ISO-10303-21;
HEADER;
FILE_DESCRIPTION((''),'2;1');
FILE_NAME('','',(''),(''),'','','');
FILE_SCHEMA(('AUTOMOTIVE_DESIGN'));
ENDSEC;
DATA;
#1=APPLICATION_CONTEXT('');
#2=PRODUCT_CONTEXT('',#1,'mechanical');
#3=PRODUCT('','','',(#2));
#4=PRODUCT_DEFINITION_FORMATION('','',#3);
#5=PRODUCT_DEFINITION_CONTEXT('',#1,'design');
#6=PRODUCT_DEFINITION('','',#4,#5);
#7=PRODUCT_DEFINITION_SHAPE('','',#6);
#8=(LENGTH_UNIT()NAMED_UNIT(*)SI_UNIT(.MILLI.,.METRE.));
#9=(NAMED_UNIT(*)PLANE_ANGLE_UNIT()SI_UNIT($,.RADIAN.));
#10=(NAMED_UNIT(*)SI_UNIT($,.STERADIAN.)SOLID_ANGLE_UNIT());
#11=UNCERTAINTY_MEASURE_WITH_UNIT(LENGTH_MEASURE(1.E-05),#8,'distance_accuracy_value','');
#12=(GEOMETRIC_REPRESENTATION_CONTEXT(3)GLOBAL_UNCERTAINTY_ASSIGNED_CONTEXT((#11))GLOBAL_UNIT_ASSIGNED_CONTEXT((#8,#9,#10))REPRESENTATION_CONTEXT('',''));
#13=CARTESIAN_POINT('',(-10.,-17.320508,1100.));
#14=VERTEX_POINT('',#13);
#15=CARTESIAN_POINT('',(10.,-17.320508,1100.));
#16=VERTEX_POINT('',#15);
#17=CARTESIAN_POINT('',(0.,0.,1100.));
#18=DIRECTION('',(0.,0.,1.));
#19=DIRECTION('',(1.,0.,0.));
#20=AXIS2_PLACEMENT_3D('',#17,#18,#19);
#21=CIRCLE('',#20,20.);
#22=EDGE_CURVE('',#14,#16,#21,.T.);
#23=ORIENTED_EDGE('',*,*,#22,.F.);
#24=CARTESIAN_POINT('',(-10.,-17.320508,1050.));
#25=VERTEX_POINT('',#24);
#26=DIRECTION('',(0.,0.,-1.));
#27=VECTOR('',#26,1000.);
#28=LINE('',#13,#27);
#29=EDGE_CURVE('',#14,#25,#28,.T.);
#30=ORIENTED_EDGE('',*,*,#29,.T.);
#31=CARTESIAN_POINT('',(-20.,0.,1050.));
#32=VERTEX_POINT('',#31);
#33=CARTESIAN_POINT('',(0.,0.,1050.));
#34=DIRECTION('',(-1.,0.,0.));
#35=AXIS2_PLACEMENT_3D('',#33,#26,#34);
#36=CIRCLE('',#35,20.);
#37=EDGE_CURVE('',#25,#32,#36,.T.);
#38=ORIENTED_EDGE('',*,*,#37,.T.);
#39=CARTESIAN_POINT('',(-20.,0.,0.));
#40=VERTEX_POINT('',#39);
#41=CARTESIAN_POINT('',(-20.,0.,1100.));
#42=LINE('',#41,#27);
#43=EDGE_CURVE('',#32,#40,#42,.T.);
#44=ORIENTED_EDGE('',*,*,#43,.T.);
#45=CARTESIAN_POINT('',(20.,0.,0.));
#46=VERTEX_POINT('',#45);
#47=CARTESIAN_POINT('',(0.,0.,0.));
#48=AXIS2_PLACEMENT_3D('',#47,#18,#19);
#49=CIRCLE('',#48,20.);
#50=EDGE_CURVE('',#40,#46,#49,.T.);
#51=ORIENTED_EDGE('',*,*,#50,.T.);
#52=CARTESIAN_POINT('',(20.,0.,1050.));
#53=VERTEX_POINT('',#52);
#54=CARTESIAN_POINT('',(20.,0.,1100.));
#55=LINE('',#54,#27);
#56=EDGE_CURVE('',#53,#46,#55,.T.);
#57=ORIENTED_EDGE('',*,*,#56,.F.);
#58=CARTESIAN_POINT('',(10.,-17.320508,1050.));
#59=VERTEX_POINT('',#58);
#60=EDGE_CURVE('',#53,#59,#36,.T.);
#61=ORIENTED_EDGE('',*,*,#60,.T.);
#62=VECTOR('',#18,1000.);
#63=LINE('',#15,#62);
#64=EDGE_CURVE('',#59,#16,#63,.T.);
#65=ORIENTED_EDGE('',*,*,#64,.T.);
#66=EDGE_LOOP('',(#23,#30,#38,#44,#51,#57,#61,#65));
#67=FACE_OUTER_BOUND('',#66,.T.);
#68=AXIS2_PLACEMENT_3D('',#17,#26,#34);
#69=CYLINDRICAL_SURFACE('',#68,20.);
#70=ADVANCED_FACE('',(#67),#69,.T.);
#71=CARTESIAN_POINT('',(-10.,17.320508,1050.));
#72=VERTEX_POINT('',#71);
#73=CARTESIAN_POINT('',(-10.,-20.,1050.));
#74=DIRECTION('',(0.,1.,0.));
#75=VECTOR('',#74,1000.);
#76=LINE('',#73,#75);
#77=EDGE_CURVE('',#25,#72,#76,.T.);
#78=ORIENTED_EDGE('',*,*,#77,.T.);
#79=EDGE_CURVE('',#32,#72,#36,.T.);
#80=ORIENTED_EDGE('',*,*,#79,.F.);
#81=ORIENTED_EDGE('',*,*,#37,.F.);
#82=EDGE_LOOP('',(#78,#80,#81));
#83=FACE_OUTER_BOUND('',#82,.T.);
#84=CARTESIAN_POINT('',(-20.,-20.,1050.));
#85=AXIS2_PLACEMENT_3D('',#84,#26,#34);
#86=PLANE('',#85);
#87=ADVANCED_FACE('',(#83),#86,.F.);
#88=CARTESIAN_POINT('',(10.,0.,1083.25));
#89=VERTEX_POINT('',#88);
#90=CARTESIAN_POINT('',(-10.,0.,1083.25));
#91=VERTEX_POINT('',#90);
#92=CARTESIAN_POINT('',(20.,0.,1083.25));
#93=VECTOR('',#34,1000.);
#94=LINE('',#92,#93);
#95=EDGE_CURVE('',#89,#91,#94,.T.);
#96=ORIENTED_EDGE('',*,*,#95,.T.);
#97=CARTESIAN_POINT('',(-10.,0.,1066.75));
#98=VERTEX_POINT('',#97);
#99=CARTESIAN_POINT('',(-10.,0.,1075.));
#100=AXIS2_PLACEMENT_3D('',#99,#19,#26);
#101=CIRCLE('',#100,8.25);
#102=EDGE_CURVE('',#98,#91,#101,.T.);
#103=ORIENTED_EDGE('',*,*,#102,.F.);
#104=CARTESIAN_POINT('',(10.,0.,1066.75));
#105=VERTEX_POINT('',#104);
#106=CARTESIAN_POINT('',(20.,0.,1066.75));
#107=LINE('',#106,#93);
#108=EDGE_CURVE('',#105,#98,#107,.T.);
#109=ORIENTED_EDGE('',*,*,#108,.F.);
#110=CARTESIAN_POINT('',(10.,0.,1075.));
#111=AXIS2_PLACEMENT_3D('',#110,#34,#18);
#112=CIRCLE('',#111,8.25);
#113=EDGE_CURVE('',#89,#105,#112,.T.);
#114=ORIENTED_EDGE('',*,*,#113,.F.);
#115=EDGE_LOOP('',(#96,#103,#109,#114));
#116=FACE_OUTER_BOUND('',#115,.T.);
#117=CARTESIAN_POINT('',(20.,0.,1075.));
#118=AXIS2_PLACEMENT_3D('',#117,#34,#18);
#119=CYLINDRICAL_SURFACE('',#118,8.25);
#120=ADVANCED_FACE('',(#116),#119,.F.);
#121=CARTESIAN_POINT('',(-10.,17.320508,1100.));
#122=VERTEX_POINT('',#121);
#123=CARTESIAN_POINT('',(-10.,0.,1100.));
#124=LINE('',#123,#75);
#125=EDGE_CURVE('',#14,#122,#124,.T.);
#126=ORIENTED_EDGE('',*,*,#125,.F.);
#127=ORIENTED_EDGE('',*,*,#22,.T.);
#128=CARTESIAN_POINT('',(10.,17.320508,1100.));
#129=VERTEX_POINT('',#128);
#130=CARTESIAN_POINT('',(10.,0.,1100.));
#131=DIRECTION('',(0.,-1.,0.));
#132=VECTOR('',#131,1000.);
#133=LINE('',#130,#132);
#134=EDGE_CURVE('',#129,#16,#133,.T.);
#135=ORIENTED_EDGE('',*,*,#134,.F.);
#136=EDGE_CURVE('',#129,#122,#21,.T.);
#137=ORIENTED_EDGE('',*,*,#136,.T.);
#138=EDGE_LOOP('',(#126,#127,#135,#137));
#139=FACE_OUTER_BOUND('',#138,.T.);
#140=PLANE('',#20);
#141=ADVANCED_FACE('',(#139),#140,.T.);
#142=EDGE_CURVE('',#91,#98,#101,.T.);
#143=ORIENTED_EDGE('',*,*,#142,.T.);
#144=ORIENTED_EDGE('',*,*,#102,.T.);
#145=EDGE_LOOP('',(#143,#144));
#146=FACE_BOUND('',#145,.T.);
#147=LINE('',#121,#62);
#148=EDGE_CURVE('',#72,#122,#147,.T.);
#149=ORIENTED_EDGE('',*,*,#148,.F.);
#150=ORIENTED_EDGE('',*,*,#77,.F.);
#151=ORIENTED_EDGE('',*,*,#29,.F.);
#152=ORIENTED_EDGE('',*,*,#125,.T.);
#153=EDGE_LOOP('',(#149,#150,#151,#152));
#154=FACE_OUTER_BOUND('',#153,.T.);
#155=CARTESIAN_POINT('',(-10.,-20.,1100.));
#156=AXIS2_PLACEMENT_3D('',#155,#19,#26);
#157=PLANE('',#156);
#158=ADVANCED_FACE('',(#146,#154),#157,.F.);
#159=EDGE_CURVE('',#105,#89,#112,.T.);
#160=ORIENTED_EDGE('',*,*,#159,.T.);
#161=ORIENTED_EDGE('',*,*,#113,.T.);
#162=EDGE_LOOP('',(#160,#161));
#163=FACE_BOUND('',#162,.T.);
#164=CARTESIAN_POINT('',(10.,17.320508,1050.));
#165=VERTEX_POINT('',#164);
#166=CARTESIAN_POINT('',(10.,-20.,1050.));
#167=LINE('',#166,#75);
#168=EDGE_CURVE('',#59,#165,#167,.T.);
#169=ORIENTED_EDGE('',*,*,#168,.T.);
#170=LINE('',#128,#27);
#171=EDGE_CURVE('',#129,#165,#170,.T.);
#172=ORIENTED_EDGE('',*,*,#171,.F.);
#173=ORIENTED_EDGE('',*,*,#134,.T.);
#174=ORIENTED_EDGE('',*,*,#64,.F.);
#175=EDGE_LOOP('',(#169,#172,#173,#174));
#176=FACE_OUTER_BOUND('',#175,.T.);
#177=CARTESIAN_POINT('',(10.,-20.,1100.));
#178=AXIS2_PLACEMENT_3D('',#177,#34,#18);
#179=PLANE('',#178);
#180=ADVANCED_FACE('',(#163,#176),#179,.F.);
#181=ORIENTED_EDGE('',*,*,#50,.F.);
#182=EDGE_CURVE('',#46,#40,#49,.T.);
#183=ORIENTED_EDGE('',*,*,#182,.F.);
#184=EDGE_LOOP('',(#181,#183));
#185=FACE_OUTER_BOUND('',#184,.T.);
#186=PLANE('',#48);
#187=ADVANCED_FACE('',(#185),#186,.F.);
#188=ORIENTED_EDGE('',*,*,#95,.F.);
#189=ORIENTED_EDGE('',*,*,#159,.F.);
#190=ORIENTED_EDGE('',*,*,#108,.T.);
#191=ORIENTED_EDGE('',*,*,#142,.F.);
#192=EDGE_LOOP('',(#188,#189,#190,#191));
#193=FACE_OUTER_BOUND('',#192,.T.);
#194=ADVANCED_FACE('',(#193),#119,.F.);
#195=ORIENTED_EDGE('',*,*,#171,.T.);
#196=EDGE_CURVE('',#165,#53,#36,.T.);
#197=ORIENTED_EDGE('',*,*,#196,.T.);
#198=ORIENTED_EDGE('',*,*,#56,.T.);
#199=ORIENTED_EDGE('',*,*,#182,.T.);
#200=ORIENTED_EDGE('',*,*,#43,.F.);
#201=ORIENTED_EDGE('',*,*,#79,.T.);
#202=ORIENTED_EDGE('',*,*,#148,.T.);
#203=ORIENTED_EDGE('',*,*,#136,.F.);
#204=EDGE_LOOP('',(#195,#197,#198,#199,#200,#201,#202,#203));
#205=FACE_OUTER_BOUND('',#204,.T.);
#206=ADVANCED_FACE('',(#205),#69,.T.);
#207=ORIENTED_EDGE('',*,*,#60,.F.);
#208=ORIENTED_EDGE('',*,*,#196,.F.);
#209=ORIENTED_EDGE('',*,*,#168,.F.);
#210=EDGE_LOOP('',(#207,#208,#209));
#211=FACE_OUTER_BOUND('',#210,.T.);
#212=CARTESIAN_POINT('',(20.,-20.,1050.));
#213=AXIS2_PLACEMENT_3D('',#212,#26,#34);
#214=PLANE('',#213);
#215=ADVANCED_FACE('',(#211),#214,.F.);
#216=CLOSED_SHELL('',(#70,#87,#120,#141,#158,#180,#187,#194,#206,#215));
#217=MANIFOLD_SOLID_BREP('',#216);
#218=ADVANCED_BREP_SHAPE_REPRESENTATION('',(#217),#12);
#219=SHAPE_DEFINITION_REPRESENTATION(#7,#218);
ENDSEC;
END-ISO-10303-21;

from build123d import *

# Parameters (mm, degrees)
SKETCH1_R               = 20
BOSS_EXTRUDE1_DEPTH     = 1100
CUT_EXTRUDE1_DEPTH      = 1101.363576278
CUT_EXTRUDE1_DEPTH_BACK = 1101.363576278
SKETCH2_W               = 10
SKETCH2_H               = 50
CUT_EXTRUDE2_DEPTH      = 1101.590750461
CUT_EXTRUDE2_DEPTH_BACK = 1101.590750461
SKETCH3_R               = 8.25


with BuildPart() as part:
    # Sketch1 → Boss-Extrude1 (new body)
    with BuildSketch(Plane.XY):
        Circle(SKETCH1_R)
    extrude(amount=BOSS_EXTRUDE1_DEPTH)

    # Sketch2 → Cut-Extrude1 (cut, two sides: drawn at the far end of the back side and taken through both)
    with BuildSketch(Plane(origin=(0, 0, 0), x_dir=(1, 0, 0), z_dir=(0, 1, 0)).offset(-CUT_EXTRUDE1_DEPTH_BACK)):
        with Locations((-15, -1075)):
            Rectangle(SKETCH2_W, SKETCH2_H)
        with Locations((15, -1075)):
            Rectangle(SKETCH2_W, SKETCH2_H)
    extrude(amount=CUT_EXTRUDE1_DEPTH + CUT_EXTRUDE1_DEPTH_BACK, mode=Mode.SUBTRACT)

    # Sketch3 → Cut-Extrude2 (cut, two sides: drawn at the far end of the back side and taken through both)
    with BuildSketch(Plane.ZY.offset(10).offset(-CUT_EXTRUDE2_DEPTH_BACK)):
        with Locations((1075, 0)):
            Circle(SKETCH3_R)
    extrude(amount=CUT_EXTRUDE2_DEPTH + CUT_EXTRUDE2_DEPTH_BACK, mode=Mode.SUBTRACT)


solid = part.part
